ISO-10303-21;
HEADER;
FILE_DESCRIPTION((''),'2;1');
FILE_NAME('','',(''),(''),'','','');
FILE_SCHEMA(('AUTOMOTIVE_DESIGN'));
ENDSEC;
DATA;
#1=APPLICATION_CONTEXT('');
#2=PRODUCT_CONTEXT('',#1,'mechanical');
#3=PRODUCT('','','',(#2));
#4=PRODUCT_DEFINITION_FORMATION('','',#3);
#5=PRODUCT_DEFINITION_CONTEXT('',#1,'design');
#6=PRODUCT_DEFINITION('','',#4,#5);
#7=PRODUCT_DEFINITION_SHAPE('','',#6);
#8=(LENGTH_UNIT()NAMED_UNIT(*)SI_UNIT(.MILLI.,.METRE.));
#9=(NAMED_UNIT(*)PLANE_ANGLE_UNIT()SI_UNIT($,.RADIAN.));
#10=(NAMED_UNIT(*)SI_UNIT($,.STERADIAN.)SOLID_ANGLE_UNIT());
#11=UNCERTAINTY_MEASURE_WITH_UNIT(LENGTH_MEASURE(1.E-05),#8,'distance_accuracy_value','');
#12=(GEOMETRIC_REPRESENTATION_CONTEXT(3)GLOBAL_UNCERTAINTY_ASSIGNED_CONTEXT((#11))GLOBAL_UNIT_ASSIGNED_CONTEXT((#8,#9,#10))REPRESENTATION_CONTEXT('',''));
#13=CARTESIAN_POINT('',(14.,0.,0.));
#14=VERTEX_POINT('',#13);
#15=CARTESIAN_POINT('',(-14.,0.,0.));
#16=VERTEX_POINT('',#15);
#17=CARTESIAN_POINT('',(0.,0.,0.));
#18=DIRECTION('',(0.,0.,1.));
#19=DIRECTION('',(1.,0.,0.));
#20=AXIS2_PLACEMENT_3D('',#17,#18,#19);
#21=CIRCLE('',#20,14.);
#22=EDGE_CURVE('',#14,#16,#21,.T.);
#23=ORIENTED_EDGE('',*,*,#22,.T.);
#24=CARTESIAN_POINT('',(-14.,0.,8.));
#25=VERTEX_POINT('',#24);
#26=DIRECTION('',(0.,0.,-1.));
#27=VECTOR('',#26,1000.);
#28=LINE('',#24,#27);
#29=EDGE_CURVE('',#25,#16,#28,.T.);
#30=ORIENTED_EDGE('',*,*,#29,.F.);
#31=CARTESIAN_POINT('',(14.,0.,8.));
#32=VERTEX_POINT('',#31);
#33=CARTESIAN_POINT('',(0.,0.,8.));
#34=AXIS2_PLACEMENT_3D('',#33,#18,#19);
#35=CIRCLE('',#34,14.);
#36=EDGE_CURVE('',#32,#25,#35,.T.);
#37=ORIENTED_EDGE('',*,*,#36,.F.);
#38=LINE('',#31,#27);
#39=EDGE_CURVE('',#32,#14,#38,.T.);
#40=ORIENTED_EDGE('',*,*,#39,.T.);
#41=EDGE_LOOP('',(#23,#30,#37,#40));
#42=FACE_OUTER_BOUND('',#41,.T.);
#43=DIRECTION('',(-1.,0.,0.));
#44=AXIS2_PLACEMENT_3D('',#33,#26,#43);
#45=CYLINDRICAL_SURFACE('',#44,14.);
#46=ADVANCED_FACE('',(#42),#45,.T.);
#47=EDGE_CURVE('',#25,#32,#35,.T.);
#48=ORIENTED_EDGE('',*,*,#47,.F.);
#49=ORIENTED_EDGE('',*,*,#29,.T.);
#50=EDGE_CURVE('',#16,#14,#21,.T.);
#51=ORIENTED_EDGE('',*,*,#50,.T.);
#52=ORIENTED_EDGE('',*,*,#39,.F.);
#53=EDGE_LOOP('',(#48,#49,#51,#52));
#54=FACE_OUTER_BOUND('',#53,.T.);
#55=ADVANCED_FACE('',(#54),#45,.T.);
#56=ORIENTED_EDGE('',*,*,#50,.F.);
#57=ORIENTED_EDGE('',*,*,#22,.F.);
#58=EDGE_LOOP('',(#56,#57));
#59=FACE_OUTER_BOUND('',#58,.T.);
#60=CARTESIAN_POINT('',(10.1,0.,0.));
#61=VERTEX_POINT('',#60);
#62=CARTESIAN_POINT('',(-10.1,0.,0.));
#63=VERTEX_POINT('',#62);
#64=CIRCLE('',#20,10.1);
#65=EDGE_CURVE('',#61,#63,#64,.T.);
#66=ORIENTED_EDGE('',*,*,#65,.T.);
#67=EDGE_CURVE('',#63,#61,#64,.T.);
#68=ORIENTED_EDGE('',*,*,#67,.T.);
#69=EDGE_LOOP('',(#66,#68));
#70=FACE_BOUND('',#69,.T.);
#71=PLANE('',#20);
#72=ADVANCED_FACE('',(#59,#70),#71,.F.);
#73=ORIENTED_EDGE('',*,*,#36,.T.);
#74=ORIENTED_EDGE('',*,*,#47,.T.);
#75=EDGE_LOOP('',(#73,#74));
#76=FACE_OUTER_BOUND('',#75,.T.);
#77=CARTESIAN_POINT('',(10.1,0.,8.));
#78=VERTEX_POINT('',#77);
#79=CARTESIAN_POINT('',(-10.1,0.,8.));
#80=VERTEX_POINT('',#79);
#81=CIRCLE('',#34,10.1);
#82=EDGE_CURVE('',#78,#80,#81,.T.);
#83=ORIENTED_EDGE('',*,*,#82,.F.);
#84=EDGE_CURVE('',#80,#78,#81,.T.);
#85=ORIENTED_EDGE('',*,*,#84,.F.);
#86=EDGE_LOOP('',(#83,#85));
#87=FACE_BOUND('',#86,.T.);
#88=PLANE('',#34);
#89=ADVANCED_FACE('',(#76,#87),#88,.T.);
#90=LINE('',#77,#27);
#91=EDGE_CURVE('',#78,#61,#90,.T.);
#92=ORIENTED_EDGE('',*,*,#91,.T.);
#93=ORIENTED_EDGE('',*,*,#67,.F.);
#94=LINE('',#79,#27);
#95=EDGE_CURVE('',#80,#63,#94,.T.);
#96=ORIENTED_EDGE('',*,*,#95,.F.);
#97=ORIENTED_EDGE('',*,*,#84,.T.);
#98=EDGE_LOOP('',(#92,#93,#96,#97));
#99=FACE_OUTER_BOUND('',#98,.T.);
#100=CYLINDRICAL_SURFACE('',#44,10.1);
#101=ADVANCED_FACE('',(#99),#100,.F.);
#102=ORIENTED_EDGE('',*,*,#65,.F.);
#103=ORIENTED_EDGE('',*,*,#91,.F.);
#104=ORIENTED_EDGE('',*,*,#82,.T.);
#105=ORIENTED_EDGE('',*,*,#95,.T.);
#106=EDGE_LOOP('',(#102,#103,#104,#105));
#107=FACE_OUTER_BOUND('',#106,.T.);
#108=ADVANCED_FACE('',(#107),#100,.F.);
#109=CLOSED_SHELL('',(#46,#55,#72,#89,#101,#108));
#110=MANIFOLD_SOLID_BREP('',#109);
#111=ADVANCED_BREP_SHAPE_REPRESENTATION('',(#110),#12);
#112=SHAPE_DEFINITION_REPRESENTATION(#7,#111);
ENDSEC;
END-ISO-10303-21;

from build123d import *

# Parameters (mm, degrees)
SKETCH1_R           = 14
SKETCH1_R_2         = 10.1
BOSS_EXTRUDE1_DEPTH = 8


with BuildPart() as part:
    # Sketch1 → Boss-Extrude1 (new body)
    with BuildSketch(Plane.XY):
        Circle(SKETCH1_R)
        Circle(SKETCH1_R_2, mode=Mode.SUBTRACT)
    extrude(amount=BOSS_EXTRUDE1_DEPTH)


solid = part.part
